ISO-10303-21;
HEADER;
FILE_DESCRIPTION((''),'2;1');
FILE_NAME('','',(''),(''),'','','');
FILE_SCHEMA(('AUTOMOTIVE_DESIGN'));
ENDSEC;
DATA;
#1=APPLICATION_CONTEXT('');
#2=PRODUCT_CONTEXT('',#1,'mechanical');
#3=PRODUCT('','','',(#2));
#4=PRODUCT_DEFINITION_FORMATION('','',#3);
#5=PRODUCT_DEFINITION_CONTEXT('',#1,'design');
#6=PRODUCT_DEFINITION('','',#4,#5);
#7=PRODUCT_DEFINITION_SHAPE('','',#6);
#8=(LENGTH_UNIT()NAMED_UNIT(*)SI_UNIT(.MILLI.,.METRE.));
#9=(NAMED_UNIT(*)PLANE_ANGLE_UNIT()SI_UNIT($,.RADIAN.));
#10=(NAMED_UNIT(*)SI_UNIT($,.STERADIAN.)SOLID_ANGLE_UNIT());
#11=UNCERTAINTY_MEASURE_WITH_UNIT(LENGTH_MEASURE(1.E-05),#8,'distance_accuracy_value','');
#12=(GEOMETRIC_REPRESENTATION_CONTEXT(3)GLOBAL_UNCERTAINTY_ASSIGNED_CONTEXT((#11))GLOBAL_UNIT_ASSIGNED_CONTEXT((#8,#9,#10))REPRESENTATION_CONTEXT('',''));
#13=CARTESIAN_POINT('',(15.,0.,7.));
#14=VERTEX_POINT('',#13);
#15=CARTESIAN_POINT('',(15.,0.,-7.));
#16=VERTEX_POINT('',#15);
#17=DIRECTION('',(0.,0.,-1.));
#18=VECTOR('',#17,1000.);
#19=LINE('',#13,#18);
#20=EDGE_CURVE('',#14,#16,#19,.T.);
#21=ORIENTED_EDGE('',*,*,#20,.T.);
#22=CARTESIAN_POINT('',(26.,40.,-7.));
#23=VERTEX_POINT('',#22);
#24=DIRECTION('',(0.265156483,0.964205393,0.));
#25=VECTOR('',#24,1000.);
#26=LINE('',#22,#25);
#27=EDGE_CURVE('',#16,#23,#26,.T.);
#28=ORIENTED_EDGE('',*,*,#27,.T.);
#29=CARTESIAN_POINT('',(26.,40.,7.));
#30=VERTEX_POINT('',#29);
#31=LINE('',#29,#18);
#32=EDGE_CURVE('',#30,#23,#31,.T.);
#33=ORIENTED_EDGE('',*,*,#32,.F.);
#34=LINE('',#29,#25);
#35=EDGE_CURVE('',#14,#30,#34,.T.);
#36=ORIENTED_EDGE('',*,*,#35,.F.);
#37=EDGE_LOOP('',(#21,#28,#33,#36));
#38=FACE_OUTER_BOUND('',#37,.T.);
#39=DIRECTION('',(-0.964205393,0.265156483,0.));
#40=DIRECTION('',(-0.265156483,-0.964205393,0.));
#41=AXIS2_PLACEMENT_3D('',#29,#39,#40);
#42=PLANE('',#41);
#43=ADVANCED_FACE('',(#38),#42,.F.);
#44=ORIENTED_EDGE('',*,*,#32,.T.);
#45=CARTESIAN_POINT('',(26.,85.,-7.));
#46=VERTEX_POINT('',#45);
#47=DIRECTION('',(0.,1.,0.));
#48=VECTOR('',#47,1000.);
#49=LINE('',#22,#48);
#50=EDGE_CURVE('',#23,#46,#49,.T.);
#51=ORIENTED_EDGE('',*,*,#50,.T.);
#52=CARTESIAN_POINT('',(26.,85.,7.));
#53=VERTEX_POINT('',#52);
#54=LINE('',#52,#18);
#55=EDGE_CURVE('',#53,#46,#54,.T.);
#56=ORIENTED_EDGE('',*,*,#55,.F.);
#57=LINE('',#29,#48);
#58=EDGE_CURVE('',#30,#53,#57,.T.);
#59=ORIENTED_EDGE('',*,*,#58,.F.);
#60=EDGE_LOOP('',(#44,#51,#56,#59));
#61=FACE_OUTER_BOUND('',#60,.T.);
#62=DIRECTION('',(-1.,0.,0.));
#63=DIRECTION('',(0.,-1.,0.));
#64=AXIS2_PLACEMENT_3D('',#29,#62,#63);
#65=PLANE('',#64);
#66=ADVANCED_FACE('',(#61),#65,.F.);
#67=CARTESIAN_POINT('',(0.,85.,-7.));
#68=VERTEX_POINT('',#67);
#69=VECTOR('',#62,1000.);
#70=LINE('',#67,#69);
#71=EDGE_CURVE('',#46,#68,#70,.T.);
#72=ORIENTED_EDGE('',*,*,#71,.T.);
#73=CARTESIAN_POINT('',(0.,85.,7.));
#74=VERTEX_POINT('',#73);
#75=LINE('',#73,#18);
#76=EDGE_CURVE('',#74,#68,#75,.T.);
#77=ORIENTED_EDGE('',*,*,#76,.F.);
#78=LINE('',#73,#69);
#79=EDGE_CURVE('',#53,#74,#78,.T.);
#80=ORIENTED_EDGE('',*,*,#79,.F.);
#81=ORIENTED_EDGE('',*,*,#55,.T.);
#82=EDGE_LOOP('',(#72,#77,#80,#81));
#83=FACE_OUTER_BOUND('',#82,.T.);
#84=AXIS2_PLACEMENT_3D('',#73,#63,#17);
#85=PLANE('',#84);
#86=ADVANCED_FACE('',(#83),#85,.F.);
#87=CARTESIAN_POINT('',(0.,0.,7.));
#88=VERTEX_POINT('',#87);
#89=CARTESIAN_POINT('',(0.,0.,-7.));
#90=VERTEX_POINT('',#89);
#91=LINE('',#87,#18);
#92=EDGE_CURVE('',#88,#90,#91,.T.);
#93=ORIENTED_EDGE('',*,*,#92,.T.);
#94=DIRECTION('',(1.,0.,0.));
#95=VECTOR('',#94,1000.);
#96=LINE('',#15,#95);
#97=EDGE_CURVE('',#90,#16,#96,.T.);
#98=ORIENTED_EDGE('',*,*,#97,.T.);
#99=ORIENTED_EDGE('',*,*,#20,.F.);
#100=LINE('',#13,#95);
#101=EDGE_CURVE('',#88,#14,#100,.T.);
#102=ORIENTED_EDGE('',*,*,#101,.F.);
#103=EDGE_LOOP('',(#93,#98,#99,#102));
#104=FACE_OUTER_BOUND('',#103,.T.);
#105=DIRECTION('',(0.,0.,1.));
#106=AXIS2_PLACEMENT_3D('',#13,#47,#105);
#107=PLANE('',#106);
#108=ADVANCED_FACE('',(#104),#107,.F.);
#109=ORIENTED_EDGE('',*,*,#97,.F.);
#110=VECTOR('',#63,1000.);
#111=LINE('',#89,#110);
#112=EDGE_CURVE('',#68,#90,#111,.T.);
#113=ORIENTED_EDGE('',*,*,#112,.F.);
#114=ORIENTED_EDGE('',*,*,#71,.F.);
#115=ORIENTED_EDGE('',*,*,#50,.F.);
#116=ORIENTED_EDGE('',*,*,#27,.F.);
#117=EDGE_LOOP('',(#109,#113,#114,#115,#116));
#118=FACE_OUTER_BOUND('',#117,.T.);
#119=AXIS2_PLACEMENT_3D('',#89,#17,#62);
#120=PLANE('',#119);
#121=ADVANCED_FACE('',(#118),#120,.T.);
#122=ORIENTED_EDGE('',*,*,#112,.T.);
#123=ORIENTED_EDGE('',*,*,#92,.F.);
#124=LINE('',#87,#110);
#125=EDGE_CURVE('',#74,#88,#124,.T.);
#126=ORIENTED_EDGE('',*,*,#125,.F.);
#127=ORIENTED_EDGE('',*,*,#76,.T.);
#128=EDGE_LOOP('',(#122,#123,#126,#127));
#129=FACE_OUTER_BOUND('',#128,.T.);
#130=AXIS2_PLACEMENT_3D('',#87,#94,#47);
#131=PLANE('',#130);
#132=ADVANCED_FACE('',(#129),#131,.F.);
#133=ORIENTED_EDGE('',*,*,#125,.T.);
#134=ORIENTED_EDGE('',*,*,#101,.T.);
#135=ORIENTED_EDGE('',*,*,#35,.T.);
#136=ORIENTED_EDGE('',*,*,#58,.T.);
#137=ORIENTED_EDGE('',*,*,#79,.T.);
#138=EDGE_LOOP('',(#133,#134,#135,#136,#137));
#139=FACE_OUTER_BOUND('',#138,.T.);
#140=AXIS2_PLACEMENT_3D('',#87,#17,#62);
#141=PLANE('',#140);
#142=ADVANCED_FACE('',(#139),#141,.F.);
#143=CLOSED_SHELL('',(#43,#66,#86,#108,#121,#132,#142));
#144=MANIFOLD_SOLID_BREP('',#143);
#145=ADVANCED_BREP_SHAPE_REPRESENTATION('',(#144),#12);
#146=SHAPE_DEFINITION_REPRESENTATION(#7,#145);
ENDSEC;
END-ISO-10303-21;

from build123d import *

# Parameters (mm, degrees)
EXTRUDE_1_DEPTH = 7


with BuildPart() as part:
    # 草图1 → 凸台-拉伸1 (new, symmetric)
    with BuildSketch(Plane.XY):
        Polygon((0, 0), (0, 85), (26, 85), (26, 40), (15, 0), align=None)
    extrude(amount=EXTRUDE_1_DEPTH, both=True)


solid = part.part
